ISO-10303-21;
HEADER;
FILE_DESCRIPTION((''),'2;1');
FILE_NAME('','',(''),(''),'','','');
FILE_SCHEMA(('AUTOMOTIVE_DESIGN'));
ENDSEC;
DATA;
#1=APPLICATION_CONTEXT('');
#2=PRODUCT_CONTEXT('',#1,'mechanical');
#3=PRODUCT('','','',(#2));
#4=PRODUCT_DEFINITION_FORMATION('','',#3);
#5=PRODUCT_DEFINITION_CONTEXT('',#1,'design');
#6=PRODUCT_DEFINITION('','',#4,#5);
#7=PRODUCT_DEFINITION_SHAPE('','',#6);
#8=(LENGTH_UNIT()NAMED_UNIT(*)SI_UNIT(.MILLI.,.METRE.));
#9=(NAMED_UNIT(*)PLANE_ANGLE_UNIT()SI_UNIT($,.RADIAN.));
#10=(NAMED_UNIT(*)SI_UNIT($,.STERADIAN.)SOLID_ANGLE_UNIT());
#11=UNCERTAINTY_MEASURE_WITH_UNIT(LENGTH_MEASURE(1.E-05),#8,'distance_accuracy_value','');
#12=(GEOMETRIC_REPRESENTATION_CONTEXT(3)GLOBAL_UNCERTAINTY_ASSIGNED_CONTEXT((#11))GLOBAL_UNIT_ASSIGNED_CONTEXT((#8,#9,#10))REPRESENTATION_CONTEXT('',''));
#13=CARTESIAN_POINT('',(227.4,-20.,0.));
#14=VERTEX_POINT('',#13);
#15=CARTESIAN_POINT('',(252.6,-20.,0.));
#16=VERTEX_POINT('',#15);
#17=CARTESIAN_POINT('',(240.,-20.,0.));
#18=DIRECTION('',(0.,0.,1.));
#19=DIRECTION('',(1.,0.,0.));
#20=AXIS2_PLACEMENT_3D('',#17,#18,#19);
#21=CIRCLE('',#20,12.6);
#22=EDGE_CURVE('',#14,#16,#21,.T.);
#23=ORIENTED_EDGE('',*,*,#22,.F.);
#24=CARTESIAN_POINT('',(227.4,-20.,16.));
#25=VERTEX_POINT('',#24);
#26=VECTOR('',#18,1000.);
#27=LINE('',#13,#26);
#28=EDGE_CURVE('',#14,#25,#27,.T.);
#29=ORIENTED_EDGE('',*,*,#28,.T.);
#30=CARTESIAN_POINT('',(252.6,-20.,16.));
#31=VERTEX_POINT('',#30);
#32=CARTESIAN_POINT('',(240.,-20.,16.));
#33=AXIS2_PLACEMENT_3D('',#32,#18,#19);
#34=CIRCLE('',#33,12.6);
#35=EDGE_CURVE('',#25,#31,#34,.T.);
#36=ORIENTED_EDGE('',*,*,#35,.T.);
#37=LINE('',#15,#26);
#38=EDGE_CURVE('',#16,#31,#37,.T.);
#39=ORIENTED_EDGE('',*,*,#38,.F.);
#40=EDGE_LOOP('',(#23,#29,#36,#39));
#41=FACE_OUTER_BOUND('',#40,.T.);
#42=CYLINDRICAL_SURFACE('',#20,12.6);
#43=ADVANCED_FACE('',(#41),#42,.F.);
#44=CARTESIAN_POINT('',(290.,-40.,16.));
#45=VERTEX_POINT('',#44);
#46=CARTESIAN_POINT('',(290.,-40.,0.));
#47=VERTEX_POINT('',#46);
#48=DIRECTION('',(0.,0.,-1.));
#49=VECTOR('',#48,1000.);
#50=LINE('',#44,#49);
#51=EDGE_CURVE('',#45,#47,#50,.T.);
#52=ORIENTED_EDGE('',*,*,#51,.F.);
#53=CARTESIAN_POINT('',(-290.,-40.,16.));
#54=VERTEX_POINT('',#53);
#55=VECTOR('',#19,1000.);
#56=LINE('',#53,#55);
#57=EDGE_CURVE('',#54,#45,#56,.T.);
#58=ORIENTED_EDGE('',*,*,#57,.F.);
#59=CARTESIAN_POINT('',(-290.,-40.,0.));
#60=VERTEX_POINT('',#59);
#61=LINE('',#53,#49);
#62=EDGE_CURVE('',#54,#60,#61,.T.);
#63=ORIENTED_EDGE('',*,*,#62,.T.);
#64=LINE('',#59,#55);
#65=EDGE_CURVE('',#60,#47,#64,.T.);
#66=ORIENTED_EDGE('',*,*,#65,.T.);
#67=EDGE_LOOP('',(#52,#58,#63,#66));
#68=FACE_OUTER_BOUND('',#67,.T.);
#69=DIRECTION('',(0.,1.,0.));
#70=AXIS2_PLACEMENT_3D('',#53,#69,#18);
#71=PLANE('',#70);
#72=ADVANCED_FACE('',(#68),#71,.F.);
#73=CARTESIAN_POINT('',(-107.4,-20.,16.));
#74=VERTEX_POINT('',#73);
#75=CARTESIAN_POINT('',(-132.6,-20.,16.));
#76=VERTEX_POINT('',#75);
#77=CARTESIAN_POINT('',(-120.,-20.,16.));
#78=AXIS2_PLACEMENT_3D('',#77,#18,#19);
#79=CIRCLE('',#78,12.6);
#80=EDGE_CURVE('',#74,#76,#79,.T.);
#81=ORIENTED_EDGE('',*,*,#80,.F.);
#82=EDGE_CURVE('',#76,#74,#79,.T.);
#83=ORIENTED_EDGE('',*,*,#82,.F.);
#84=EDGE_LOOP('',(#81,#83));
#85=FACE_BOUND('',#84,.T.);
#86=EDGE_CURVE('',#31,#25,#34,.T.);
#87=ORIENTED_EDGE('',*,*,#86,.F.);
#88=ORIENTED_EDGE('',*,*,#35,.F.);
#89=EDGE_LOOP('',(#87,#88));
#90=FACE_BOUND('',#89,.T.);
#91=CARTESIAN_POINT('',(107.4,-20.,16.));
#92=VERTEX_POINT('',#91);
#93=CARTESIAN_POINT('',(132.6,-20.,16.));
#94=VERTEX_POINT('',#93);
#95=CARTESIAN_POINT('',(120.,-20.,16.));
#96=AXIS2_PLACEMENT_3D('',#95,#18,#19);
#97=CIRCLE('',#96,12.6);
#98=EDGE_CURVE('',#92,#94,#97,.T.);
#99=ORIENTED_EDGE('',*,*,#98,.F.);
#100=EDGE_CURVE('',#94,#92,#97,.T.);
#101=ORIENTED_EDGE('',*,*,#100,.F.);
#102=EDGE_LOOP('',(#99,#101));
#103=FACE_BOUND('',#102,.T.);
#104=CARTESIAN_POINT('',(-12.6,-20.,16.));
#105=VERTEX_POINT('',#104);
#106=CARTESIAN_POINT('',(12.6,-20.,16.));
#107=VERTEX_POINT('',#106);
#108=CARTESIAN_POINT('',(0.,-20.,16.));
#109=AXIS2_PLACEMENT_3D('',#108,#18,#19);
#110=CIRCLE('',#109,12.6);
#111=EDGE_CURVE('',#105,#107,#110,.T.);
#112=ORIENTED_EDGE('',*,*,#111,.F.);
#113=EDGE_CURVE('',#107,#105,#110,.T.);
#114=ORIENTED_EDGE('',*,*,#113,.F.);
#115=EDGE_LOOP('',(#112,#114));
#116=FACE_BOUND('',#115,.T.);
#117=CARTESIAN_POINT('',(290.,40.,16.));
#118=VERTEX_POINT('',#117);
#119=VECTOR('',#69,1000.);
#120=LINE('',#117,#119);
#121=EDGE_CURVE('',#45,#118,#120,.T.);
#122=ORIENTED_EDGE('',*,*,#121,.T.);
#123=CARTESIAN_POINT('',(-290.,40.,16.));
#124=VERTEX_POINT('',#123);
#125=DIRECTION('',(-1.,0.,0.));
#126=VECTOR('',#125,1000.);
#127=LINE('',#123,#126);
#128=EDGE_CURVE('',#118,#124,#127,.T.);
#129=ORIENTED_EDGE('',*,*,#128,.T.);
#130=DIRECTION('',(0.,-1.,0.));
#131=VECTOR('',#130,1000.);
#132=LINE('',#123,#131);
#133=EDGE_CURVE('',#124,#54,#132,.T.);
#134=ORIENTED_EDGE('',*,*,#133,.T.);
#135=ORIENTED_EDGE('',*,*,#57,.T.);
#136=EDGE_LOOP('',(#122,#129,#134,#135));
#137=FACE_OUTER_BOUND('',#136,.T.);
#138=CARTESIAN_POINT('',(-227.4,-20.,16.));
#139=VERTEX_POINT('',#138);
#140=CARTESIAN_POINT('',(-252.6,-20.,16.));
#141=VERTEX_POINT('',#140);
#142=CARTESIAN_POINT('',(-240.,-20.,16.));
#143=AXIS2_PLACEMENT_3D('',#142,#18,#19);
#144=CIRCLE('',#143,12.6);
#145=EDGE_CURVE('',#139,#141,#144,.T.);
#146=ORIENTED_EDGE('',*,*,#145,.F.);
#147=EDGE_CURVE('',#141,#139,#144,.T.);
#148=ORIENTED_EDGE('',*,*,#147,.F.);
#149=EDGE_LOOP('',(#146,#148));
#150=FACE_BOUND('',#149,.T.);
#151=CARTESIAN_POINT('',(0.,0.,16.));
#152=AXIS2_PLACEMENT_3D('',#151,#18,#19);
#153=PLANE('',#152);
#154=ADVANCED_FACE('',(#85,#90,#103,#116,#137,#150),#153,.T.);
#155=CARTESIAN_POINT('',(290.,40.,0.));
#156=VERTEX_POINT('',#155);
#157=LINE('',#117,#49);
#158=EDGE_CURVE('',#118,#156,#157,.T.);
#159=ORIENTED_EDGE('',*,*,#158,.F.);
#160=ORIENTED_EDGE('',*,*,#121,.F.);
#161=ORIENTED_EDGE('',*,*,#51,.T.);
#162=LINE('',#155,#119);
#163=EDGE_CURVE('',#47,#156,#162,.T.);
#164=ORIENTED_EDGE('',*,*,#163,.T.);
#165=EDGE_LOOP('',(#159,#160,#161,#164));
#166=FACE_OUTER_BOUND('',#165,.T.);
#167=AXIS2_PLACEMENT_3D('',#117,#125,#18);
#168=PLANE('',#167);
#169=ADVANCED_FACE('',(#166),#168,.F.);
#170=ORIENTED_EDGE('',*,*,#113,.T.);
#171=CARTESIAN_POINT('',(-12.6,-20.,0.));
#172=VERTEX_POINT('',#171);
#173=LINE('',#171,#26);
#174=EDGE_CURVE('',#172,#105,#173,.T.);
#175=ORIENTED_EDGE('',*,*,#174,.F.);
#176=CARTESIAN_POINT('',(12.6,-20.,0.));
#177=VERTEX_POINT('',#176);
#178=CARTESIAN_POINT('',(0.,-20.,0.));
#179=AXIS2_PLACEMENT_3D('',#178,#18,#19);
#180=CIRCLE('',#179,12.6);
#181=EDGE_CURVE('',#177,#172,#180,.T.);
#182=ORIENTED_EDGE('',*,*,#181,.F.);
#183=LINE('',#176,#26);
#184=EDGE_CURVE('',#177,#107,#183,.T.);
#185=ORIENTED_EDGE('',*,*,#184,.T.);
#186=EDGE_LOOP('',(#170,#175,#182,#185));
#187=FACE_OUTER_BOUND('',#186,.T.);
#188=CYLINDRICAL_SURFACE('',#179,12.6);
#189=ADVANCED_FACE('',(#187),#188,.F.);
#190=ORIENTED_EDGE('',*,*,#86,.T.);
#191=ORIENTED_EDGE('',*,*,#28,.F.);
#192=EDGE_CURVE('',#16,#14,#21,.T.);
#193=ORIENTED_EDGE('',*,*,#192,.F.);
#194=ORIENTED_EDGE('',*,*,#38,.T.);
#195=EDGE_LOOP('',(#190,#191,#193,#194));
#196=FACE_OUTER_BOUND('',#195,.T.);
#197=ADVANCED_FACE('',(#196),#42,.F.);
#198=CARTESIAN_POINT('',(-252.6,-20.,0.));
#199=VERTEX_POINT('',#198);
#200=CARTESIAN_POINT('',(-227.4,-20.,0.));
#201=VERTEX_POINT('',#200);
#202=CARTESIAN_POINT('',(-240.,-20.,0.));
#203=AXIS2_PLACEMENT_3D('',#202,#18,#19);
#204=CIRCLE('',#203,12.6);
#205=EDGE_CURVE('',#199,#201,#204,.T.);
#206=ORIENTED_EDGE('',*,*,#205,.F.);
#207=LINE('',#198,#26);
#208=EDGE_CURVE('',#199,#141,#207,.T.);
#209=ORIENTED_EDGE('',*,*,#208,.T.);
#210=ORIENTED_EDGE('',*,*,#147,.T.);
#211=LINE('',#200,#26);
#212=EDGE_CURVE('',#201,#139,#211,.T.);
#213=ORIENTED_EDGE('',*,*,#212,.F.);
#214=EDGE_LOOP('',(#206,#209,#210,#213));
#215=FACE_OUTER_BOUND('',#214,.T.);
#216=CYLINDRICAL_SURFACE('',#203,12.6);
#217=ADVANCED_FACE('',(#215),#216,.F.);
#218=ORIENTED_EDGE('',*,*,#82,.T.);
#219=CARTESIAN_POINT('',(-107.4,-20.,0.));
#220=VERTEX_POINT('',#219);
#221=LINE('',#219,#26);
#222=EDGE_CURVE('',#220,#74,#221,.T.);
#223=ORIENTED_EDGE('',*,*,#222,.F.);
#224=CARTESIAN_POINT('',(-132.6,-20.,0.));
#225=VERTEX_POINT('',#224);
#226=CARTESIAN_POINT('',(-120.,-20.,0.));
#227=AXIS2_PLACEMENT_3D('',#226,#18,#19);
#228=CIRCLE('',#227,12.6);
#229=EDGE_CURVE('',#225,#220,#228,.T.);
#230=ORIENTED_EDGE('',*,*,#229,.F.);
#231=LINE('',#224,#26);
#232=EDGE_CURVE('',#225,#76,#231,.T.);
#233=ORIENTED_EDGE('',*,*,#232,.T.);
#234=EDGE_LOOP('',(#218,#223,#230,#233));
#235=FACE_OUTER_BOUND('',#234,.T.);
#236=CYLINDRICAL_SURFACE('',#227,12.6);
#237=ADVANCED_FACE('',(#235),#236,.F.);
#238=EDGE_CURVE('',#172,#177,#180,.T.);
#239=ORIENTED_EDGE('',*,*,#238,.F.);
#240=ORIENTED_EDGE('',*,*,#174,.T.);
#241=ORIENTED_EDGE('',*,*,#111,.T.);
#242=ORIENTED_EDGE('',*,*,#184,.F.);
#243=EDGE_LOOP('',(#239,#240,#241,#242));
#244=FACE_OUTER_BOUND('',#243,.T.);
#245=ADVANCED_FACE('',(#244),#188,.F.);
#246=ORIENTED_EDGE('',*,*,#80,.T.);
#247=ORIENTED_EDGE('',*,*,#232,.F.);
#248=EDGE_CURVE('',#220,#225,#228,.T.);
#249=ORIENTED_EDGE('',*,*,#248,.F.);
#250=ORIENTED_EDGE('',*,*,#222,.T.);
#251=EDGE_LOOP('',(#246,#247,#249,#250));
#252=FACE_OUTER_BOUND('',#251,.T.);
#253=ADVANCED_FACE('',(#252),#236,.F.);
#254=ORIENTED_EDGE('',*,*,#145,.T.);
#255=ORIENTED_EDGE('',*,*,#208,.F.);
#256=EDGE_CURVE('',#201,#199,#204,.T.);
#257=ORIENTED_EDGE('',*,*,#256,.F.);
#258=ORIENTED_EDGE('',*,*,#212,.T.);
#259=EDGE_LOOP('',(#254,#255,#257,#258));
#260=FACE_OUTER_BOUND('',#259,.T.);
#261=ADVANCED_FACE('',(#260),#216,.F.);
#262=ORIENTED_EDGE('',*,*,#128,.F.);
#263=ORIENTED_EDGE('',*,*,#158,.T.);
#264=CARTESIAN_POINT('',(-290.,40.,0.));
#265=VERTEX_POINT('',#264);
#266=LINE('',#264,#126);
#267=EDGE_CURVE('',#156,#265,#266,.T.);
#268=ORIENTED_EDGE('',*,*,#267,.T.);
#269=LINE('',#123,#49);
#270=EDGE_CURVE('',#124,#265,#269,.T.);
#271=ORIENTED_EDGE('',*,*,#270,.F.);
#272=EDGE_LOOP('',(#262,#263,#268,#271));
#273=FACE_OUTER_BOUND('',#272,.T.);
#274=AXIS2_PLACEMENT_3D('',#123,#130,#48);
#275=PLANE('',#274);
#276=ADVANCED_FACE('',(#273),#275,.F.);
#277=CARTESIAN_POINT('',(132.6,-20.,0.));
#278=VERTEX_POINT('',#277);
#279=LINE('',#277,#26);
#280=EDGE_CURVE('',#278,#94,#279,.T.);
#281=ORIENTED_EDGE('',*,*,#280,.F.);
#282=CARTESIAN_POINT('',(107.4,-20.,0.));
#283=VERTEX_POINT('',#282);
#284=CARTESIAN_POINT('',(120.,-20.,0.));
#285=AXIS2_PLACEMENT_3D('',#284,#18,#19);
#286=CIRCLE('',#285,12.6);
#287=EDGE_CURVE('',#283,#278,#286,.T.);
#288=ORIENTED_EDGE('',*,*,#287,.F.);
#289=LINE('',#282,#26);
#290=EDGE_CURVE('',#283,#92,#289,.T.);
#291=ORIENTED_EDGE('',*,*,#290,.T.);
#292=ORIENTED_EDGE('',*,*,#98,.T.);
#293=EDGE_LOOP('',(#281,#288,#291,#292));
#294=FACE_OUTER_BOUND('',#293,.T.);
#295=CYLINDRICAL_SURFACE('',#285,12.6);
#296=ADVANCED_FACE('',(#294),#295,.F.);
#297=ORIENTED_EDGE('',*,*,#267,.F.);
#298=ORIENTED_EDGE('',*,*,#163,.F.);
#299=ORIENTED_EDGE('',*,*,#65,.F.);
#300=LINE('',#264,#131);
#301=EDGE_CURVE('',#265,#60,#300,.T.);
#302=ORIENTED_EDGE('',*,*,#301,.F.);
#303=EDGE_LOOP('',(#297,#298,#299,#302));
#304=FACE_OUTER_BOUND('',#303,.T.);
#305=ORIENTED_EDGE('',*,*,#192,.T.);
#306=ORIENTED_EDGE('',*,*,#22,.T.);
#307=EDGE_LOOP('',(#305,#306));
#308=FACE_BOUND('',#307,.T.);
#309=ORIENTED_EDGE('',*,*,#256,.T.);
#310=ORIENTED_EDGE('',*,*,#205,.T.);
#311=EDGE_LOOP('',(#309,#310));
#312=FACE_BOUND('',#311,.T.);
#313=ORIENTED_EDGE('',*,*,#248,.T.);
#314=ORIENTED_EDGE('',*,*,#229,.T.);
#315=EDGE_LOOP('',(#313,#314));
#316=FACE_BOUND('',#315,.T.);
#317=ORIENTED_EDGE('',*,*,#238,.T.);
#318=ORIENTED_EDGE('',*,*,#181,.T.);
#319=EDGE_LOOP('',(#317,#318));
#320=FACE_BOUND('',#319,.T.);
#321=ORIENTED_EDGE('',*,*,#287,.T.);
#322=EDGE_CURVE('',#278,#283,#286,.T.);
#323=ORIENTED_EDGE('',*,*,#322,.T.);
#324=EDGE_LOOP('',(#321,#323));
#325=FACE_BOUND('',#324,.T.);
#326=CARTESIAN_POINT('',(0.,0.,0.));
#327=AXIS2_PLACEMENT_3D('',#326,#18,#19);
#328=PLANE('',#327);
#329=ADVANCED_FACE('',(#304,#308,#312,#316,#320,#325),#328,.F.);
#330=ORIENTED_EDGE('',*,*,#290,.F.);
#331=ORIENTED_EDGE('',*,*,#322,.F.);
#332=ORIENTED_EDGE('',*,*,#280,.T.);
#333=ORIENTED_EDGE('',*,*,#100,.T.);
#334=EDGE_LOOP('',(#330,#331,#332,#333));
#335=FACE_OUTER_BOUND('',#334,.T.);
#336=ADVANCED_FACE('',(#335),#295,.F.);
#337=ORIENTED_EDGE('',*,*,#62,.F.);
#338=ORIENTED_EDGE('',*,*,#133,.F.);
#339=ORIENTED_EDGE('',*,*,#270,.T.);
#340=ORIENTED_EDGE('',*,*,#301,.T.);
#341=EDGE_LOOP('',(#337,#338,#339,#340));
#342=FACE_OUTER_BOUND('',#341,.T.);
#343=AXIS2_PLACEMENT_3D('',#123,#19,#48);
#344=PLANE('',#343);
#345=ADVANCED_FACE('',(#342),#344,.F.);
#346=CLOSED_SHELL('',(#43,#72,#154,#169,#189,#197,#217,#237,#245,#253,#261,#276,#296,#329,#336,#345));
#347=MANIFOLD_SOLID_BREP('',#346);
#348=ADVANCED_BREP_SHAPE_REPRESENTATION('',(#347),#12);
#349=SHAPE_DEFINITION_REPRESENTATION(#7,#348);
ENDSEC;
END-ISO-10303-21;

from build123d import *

# Parameters (mm, degrees)
BAR_PROFILE_SKETCH_W      = 580
BAR_PROFILE_SKETCH_H      = 80
FLAT_BAR_580X80X16_DEPTH  = 16
HOLE_ROW_SKETCH_R         = 12.6
THROUGH_HOLES_5X_20_DEPTH = 16


with BuildPart() as part:
    # Bar Profile Sketch → Flat Bar 580x80x16 (new body)
    with BuildSketch(Plane.XY):
        Rectangle(BAR_PROFILE_SKETCH_W, BAR_PROFILE_SKETCH_H)
    extrude(amount=FLAT_BAR_580X80X16_DEPTH)

    # Hole Row Sketch → Through Holes 5xØ20 (cut)
    with BuildSketch(Plane.XY.offset(16)):
        with Locations((-240, -20)):
            Circle(HOLE_ROW_SKETCH_R)
        with Locations((-120, -20)):
            Circle(HOLE_ROW_SKETCH_R)
        with Locations((0, -20)):
            Circle(HOLE_ROW_SKETCH_R)
        with Locations((120, -20)):
            Circle(HOLE_ROW_SKETCH_R)
        with Locations((240, -20)):
            Circle(HOLE_ROW_SKETCH_R)
    extrude(amount=-THROUGH_HOLES_5X_20_DEPTH, mode=Mode.SUBTRACT)


solid = part.part
